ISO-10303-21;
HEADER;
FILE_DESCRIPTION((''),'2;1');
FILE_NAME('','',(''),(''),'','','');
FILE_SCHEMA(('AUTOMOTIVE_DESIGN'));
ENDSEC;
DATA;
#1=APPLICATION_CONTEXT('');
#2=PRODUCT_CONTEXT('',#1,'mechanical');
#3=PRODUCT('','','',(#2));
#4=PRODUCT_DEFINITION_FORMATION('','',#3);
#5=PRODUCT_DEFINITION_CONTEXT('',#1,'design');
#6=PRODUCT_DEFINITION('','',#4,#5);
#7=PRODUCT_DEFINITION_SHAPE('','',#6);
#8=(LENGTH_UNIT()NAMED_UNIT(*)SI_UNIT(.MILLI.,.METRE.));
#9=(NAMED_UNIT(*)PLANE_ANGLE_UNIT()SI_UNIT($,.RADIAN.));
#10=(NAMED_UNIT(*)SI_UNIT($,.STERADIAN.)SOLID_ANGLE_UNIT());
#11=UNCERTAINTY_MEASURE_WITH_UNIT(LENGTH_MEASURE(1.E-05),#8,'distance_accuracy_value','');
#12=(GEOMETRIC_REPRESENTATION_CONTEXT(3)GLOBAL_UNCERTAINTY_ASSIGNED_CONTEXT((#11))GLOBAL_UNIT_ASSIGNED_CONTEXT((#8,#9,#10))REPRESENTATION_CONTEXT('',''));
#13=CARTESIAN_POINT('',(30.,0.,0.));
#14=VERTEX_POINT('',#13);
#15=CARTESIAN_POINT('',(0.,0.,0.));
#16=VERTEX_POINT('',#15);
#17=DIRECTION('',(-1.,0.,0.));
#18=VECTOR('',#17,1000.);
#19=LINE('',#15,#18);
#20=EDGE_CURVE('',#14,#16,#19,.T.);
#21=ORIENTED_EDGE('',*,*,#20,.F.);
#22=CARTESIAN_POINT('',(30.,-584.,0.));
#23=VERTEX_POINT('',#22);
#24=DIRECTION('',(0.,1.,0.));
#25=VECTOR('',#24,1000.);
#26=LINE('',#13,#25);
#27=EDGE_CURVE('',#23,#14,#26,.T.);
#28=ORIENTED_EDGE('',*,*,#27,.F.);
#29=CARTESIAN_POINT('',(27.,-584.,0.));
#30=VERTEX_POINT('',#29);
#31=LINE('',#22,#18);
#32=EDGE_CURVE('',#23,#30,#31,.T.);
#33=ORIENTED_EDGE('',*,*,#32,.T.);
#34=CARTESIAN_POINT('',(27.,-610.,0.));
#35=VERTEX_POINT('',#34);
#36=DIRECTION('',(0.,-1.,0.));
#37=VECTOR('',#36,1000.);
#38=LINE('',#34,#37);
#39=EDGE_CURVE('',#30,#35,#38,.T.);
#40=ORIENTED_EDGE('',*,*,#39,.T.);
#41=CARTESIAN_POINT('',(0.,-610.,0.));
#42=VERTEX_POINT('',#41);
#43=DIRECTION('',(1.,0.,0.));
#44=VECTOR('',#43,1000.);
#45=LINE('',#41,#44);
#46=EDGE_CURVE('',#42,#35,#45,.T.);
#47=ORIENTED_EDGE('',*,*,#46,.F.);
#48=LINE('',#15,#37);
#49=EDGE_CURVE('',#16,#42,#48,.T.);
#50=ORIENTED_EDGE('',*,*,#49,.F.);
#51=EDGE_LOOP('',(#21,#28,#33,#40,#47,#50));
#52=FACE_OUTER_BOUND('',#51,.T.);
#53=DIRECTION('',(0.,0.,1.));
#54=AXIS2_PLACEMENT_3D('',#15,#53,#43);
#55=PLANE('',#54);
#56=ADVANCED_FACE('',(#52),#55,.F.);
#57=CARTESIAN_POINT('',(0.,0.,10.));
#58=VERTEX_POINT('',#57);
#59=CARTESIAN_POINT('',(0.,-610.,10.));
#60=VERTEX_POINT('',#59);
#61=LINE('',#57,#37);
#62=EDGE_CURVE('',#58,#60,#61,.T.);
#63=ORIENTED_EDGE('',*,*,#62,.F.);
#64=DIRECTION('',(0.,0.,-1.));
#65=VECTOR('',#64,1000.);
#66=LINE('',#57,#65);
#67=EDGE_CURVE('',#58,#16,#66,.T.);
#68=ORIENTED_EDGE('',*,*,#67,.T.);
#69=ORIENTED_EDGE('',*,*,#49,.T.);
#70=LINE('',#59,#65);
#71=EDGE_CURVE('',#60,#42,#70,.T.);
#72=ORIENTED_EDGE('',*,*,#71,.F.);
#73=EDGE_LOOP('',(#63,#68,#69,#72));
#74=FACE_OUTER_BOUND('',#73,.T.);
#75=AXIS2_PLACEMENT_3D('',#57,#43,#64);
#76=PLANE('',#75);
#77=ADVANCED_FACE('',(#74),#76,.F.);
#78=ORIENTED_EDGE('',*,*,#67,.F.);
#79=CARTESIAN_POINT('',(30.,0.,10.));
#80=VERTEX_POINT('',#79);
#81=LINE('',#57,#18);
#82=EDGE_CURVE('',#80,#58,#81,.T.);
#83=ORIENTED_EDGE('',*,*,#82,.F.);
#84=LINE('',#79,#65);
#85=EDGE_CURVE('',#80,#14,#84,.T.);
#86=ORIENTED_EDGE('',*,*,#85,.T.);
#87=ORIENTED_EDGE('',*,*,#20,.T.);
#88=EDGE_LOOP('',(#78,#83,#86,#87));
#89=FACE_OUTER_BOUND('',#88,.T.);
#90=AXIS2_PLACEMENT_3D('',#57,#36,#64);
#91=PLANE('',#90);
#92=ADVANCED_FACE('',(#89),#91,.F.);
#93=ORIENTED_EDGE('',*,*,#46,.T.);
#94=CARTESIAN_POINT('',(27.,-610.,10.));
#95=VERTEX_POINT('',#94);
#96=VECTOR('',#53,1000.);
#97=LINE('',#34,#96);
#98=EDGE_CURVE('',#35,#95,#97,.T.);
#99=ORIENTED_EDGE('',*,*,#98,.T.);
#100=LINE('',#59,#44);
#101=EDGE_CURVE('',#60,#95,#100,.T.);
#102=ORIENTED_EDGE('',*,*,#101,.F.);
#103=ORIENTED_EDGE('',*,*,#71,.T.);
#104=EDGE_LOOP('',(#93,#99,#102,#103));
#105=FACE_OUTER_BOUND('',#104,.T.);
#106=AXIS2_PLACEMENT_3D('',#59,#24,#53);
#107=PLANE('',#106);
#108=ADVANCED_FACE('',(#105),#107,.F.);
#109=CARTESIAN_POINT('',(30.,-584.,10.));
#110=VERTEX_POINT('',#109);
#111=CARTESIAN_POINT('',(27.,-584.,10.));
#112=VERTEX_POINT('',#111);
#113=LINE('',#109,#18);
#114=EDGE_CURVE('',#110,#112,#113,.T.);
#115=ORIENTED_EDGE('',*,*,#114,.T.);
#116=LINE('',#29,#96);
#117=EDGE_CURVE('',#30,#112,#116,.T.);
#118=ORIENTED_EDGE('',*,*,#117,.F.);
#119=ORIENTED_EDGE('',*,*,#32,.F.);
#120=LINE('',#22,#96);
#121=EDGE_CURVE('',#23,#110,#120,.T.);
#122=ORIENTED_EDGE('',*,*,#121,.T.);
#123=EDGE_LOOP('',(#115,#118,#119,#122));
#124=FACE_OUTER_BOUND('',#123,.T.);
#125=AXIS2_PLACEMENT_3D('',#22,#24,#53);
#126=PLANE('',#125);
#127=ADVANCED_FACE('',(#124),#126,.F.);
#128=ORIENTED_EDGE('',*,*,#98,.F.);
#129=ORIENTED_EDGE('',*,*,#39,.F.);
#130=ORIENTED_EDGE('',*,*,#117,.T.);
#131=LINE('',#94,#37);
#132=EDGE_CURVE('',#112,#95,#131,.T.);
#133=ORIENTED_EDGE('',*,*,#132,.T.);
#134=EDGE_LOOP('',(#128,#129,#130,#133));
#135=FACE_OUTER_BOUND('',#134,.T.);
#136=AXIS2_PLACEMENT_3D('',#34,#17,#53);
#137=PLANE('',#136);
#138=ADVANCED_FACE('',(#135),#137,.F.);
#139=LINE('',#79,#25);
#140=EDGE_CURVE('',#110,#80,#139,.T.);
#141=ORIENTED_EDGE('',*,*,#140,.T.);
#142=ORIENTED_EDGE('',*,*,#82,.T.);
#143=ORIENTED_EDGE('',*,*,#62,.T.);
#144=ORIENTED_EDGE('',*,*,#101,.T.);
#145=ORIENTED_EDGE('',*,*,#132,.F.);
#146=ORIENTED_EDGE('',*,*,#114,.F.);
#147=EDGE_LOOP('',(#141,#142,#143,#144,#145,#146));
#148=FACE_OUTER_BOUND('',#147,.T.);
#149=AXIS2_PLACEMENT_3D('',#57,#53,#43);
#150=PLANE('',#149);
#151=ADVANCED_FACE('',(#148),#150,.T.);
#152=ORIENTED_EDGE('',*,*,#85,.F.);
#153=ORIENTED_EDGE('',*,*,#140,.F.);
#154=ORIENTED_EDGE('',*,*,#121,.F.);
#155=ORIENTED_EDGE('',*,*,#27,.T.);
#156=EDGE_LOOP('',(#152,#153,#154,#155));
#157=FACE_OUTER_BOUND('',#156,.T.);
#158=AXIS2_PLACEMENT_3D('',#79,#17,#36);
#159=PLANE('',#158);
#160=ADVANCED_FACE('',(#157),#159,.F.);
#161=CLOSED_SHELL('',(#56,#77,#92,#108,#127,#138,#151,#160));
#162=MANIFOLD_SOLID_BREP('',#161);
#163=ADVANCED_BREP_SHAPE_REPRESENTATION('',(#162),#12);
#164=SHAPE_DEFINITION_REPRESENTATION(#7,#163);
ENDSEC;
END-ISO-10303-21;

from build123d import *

# Parameters (mm, degrees)
SKETCH1_W           = 30
SKETCH1_H           = 610
BOSS_EXTRUDE1_DEPTH = 10
SKETCH2_W           = 3
SKETCH2_H           = 26
CUT_EXTRUDE1_DEPTH  = 10


with BuildPart() as part:
    # Sketch1 → Boss-Extrude1 (new body)
    with BuildSketch(Plane.XY):
        with Locations((15, -305)):
            Rectangle(SKETCH1_W, SKETCH1_H)
    extrude(amount=BOSS_EXTRUDE1_DEPTH)

    # Sketch2 → Cut-Extrude1 (cut)
    with BuildSketch(Plane.XY.offset(10)):
        with Locations((28.5, -597)):
            Rectangle(SKETCH2_W, SKETCH2_H)
    extrude(amount=-CUT_EXTRUDE1_DEPTH, mode=Mode.SUBTRACT)


solid = part.part
